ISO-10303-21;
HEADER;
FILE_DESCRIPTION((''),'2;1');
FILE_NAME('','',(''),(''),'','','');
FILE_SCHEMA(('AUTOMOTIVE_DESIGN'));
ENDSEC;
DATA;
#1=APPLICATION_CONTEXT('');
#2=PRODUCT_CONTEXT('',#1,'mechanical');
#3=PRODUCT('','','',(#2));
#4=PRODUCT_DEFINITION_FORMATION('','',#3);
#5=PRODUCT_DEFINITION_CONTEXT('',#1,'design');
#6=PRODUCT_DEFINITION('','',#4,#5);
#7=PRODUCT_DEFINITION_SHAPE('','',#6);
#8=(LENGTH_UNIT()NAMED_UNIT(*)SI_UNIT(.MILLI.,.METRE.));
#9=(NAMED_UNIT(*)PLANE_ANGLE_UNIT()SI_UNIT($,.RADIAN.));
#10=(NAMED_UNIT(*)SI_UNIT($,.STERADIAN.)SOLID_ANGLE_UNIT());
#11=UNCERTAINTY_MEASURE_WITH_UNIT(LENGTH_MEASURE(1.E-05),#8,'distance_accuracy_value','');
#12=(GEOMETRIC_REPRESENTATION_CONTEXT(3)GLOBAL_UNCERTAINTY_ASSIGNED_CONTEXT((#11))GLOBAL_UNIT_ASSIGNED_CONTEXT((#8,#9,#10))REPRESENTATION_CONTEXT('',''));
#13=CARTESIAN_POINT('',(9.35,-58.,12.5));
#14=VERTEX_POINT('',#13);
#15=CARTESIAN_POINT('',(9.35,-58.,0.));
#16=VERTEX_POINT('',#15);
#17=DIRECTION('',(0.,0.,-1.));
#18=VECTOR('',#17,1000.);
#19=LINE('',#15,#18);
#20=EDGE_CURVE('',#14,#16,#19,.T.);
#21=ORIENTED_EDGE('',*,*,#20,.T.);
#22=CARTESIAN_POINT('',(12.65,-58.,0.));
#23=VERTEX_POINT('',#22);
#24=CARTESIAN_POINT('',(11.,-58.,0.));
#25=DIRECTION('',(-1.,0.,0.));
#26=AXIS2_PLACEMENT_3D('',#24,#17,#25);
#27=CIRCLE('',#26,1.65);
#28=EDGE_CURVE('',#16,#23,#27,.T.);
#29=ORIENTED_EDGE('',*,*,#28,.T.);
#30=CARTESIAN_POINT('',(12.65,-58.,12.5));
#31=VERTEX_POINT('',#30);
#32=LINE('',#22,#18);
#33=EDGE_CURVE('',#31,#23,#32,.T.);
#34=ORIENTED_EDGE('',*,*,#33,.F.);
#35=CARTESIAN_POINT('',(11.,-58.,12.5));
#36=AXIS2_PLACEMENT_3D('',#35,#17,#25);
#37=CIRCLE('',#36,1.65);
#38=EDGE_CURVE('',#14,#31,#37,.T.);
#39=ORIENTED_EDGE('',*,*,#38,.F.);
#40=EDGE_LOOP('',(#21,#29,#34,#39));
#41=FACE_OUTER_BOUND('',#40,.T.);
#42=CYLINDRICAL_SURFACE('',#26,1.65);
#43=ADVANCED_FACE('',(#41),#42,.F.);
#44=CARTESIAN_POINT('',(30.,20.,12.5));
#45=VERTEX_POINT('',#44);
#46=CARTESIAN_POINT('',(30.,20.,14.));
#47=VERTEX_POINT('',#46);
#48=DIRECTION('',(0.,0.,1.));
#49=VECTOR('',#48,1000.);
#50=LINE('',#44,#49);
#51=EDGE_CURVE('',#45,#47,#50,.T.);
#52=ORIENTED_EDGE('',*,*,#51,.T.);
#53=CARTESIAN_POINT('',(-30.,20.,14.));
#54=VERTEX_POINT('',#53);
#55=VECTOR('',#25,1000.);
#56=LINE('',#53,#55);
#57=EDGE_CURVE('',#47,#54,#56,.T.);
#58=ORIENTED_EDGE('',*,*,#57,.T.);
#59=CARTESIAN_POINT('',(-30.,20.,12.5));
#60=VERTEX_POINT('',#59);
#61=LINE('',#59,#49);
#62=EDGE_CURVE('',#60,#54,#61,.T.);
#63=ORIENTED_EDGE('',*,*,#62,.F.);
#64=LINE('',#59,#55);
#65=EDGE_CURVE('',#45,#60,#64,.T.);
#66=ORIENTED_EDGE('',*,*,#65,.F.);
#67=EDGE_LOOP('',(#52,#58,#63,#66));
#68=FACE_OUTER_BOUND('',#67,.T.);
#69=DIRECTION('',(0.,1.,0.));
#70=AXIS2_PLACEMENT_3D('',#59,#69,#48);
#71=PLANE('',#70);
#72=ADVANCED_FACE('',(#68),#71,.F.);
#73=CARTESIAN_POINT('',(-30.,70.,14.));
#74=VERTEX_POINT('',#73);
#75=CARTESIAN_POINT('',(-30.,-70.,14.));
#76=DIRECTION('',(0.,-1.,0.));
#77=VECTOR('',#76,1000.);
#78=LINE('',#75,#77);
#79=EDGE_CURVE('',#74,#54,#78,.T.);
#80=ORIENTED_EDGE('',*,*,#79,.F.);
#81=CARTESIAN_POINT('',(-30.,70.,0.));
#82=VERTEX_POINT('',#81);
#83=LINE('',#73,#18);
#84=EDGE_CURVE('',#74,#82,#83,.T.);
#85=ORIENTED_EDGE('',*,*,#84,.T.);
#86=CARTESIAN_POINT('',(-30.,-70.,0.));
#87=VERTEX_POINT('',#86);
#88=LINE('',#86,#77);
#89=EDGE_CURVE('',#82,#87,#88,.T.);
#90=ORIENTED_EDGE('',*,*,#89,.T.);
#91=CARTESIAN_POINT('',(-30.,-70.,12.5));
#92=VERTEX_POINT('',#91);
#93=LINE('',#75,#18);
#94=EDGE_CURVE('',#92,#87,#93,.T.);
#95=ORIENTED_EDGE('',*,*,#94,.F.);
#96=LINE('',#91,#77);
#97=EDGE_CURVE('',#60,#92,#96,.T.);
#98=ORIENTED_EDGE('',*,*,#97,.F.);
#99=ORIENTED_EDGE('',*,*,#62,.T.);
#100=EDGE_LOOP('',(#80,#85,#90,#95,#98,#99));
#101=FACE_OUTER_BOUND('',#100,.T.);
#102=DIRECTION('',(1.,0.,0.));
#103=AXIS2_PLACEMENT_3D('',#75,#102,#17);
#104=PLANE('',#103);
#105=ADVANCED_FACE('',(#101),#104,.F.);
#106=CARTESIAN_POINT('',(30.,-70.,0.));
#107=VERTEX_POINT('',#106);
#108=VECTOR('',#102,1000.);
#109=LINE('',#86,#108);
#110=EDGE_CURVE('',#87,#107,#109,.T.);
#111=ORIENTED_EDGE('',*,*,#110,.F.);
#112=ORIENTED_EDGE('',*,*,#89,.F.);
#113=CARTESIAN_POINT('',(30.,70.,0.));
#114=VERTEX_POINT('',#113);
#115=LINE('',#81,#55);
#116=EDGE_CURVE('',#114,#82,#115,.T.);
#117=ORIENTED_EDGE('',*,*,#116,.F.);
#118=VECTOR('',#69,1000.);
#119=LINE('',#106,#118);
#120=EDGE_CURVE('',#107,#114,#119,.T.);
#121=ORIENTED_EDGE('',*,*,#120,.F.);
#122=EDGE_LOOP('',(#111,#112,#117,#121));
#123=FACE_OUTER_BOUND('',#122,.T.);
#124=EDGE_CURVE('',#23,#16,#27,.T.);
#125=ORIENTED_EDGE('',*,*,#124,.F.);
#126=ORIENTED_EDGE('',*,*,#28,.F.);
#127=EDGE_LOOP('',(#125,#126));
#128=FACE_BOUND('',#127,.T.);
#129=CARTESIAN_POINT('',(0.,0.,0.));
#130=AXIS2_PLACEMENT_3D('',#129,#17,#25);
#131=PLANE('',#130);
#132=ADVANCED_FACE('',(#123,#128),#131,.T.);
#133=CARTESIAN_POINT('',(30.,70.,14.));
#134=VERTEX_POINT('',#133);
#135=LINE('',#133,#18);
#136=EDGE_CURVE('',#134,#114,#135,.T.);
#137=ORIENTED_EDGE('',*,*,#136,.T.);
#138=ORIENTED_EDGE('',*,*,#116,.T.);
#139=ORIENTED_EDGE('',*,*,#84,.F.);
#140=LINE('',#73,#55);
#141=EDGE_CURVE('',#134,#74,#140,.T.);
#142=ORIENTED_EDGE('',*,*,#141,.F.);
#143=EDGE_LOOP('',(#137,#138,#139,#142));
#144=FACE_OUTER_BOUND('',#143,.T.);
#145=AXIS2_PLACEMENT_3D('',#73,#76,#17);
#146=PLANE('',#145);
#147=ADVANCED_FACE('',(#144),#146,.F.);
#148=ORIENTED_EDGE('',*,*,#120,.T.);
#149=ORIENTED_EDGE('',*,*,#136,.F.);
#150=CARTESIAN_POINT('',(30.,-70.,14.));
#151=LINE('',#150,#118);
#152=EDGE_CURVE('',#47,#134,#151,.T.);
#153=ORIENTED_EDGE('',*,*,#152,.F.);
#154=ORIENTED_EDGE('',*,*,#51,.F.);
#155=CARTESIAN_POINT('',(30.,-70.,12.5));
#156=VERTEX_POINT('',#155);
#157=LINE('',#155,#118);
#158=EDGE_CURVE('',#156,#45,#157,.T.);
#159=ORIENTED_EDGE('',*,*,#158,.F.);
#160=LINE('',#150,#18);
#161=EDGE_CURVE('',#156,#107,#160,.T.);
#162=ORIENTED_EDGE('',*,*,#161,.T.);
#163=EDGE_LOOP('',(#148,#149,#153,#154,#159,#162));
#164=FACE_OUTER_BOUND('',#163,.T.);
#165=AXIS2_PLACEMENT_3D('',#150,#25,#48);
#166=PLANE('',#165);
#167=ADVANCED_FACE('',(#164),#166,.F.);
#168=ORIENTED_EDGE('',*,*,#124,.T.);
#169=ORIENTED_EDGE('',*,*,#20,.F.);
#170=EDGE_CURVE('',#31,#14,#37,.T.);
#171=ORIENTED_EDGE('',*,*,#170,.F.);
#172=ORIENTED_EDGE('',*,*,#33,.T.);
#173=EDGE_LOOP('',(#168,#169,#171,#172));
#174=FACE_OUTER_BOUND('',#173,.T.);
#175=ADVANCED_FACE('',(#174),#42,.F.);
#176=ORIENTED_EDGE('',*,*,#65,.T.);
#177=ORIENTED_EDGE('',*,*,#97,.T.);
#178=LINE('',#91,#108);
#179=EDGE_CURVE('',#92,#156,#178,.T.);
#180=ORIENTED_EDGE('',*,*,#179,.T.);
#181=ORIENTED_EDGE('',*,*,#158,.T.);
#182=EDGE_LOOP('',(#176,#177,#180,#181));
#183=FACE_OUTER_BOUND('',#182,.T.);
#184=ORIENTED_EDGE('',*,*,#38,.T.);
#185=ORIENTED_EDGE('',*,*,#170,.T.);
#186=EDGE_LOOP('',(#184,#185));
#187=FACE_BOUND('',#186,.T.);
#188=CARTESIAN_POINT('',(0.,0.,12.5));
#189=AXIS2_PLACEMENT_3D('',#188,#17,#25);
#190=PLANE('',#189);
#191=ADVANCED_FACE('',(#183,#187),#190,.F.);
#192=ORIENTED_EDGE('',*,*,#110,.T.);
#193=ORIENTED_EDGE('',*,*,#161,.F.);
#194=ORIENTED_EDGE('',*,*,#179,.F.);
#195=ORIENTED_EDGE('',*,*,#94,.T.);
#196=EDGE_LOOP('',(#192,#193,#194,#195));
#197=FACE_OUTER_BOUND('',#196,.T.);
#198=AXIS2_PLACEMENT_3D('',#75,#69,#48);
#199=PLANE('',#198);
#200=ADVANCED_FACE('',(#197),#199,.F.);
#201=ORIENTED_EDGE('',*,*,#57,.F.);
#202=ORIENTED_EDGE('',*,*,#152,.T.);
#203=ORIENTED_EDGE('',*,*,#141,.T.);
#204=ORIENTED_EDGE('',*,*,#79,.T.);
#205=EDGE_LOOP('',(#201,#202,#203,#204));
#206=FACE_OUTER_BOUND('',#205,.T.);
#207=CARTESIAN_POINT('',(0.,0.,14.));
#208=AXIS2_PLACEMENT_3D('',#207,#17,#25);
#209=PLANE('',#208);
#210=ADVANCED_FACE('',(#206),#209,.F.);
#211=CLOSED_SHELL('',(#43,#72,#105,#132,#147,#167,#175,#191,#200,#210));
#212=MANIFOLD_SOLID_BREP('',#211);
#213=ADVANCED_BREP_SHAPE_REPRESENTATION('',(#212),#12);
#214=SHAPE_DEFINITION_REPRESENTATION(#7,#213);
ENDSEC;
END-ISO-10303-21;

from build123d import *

# Parameters (mm, degrees)
SKETCH_1_W          = 60
SKETCH_1_H          = 140
EXTRUDE_1_DEPTH     = 14
SKETCH_2_W          = 60
SKETCH_2_H          = 90
CUT_EXTRUDE_1_DEPTH = 1.5
HOLE_WIZARD_M4_1_D  = 3.3


with BuildPart() as part:
    # 草图1 → 凸台-拉伸1 (new body)
    with BuildSketch(Plane.XY):
        Rectangle(SKETCH_1_W, SKETCH_1_H)
    extrude(amount=EXTRUDE_1_DEPTH)

    # 草图2 → 切除-拉伸1 (cut)
    with BuildSketch(Plane.XY.offset(14)):
        with Locations((0, -25)):
            Rectangle(SKETCH_2_W, SKETCH_2_H)
    extrude(amount=-CUT_EXTRUDE_1_DEPTH, mode=Mode.SUBTRACT)

    # M4 螺纹孔1 (through all)
    with Locations(Plane(origin=(0, 0, 0), x_dir=(-1, 0, 0), z_dir=(0, 0, -1))):
        with Locations((-11, -58)):
            Hole(HOLE_WIZARD_M4_1_D / 2)


solid = part.part
